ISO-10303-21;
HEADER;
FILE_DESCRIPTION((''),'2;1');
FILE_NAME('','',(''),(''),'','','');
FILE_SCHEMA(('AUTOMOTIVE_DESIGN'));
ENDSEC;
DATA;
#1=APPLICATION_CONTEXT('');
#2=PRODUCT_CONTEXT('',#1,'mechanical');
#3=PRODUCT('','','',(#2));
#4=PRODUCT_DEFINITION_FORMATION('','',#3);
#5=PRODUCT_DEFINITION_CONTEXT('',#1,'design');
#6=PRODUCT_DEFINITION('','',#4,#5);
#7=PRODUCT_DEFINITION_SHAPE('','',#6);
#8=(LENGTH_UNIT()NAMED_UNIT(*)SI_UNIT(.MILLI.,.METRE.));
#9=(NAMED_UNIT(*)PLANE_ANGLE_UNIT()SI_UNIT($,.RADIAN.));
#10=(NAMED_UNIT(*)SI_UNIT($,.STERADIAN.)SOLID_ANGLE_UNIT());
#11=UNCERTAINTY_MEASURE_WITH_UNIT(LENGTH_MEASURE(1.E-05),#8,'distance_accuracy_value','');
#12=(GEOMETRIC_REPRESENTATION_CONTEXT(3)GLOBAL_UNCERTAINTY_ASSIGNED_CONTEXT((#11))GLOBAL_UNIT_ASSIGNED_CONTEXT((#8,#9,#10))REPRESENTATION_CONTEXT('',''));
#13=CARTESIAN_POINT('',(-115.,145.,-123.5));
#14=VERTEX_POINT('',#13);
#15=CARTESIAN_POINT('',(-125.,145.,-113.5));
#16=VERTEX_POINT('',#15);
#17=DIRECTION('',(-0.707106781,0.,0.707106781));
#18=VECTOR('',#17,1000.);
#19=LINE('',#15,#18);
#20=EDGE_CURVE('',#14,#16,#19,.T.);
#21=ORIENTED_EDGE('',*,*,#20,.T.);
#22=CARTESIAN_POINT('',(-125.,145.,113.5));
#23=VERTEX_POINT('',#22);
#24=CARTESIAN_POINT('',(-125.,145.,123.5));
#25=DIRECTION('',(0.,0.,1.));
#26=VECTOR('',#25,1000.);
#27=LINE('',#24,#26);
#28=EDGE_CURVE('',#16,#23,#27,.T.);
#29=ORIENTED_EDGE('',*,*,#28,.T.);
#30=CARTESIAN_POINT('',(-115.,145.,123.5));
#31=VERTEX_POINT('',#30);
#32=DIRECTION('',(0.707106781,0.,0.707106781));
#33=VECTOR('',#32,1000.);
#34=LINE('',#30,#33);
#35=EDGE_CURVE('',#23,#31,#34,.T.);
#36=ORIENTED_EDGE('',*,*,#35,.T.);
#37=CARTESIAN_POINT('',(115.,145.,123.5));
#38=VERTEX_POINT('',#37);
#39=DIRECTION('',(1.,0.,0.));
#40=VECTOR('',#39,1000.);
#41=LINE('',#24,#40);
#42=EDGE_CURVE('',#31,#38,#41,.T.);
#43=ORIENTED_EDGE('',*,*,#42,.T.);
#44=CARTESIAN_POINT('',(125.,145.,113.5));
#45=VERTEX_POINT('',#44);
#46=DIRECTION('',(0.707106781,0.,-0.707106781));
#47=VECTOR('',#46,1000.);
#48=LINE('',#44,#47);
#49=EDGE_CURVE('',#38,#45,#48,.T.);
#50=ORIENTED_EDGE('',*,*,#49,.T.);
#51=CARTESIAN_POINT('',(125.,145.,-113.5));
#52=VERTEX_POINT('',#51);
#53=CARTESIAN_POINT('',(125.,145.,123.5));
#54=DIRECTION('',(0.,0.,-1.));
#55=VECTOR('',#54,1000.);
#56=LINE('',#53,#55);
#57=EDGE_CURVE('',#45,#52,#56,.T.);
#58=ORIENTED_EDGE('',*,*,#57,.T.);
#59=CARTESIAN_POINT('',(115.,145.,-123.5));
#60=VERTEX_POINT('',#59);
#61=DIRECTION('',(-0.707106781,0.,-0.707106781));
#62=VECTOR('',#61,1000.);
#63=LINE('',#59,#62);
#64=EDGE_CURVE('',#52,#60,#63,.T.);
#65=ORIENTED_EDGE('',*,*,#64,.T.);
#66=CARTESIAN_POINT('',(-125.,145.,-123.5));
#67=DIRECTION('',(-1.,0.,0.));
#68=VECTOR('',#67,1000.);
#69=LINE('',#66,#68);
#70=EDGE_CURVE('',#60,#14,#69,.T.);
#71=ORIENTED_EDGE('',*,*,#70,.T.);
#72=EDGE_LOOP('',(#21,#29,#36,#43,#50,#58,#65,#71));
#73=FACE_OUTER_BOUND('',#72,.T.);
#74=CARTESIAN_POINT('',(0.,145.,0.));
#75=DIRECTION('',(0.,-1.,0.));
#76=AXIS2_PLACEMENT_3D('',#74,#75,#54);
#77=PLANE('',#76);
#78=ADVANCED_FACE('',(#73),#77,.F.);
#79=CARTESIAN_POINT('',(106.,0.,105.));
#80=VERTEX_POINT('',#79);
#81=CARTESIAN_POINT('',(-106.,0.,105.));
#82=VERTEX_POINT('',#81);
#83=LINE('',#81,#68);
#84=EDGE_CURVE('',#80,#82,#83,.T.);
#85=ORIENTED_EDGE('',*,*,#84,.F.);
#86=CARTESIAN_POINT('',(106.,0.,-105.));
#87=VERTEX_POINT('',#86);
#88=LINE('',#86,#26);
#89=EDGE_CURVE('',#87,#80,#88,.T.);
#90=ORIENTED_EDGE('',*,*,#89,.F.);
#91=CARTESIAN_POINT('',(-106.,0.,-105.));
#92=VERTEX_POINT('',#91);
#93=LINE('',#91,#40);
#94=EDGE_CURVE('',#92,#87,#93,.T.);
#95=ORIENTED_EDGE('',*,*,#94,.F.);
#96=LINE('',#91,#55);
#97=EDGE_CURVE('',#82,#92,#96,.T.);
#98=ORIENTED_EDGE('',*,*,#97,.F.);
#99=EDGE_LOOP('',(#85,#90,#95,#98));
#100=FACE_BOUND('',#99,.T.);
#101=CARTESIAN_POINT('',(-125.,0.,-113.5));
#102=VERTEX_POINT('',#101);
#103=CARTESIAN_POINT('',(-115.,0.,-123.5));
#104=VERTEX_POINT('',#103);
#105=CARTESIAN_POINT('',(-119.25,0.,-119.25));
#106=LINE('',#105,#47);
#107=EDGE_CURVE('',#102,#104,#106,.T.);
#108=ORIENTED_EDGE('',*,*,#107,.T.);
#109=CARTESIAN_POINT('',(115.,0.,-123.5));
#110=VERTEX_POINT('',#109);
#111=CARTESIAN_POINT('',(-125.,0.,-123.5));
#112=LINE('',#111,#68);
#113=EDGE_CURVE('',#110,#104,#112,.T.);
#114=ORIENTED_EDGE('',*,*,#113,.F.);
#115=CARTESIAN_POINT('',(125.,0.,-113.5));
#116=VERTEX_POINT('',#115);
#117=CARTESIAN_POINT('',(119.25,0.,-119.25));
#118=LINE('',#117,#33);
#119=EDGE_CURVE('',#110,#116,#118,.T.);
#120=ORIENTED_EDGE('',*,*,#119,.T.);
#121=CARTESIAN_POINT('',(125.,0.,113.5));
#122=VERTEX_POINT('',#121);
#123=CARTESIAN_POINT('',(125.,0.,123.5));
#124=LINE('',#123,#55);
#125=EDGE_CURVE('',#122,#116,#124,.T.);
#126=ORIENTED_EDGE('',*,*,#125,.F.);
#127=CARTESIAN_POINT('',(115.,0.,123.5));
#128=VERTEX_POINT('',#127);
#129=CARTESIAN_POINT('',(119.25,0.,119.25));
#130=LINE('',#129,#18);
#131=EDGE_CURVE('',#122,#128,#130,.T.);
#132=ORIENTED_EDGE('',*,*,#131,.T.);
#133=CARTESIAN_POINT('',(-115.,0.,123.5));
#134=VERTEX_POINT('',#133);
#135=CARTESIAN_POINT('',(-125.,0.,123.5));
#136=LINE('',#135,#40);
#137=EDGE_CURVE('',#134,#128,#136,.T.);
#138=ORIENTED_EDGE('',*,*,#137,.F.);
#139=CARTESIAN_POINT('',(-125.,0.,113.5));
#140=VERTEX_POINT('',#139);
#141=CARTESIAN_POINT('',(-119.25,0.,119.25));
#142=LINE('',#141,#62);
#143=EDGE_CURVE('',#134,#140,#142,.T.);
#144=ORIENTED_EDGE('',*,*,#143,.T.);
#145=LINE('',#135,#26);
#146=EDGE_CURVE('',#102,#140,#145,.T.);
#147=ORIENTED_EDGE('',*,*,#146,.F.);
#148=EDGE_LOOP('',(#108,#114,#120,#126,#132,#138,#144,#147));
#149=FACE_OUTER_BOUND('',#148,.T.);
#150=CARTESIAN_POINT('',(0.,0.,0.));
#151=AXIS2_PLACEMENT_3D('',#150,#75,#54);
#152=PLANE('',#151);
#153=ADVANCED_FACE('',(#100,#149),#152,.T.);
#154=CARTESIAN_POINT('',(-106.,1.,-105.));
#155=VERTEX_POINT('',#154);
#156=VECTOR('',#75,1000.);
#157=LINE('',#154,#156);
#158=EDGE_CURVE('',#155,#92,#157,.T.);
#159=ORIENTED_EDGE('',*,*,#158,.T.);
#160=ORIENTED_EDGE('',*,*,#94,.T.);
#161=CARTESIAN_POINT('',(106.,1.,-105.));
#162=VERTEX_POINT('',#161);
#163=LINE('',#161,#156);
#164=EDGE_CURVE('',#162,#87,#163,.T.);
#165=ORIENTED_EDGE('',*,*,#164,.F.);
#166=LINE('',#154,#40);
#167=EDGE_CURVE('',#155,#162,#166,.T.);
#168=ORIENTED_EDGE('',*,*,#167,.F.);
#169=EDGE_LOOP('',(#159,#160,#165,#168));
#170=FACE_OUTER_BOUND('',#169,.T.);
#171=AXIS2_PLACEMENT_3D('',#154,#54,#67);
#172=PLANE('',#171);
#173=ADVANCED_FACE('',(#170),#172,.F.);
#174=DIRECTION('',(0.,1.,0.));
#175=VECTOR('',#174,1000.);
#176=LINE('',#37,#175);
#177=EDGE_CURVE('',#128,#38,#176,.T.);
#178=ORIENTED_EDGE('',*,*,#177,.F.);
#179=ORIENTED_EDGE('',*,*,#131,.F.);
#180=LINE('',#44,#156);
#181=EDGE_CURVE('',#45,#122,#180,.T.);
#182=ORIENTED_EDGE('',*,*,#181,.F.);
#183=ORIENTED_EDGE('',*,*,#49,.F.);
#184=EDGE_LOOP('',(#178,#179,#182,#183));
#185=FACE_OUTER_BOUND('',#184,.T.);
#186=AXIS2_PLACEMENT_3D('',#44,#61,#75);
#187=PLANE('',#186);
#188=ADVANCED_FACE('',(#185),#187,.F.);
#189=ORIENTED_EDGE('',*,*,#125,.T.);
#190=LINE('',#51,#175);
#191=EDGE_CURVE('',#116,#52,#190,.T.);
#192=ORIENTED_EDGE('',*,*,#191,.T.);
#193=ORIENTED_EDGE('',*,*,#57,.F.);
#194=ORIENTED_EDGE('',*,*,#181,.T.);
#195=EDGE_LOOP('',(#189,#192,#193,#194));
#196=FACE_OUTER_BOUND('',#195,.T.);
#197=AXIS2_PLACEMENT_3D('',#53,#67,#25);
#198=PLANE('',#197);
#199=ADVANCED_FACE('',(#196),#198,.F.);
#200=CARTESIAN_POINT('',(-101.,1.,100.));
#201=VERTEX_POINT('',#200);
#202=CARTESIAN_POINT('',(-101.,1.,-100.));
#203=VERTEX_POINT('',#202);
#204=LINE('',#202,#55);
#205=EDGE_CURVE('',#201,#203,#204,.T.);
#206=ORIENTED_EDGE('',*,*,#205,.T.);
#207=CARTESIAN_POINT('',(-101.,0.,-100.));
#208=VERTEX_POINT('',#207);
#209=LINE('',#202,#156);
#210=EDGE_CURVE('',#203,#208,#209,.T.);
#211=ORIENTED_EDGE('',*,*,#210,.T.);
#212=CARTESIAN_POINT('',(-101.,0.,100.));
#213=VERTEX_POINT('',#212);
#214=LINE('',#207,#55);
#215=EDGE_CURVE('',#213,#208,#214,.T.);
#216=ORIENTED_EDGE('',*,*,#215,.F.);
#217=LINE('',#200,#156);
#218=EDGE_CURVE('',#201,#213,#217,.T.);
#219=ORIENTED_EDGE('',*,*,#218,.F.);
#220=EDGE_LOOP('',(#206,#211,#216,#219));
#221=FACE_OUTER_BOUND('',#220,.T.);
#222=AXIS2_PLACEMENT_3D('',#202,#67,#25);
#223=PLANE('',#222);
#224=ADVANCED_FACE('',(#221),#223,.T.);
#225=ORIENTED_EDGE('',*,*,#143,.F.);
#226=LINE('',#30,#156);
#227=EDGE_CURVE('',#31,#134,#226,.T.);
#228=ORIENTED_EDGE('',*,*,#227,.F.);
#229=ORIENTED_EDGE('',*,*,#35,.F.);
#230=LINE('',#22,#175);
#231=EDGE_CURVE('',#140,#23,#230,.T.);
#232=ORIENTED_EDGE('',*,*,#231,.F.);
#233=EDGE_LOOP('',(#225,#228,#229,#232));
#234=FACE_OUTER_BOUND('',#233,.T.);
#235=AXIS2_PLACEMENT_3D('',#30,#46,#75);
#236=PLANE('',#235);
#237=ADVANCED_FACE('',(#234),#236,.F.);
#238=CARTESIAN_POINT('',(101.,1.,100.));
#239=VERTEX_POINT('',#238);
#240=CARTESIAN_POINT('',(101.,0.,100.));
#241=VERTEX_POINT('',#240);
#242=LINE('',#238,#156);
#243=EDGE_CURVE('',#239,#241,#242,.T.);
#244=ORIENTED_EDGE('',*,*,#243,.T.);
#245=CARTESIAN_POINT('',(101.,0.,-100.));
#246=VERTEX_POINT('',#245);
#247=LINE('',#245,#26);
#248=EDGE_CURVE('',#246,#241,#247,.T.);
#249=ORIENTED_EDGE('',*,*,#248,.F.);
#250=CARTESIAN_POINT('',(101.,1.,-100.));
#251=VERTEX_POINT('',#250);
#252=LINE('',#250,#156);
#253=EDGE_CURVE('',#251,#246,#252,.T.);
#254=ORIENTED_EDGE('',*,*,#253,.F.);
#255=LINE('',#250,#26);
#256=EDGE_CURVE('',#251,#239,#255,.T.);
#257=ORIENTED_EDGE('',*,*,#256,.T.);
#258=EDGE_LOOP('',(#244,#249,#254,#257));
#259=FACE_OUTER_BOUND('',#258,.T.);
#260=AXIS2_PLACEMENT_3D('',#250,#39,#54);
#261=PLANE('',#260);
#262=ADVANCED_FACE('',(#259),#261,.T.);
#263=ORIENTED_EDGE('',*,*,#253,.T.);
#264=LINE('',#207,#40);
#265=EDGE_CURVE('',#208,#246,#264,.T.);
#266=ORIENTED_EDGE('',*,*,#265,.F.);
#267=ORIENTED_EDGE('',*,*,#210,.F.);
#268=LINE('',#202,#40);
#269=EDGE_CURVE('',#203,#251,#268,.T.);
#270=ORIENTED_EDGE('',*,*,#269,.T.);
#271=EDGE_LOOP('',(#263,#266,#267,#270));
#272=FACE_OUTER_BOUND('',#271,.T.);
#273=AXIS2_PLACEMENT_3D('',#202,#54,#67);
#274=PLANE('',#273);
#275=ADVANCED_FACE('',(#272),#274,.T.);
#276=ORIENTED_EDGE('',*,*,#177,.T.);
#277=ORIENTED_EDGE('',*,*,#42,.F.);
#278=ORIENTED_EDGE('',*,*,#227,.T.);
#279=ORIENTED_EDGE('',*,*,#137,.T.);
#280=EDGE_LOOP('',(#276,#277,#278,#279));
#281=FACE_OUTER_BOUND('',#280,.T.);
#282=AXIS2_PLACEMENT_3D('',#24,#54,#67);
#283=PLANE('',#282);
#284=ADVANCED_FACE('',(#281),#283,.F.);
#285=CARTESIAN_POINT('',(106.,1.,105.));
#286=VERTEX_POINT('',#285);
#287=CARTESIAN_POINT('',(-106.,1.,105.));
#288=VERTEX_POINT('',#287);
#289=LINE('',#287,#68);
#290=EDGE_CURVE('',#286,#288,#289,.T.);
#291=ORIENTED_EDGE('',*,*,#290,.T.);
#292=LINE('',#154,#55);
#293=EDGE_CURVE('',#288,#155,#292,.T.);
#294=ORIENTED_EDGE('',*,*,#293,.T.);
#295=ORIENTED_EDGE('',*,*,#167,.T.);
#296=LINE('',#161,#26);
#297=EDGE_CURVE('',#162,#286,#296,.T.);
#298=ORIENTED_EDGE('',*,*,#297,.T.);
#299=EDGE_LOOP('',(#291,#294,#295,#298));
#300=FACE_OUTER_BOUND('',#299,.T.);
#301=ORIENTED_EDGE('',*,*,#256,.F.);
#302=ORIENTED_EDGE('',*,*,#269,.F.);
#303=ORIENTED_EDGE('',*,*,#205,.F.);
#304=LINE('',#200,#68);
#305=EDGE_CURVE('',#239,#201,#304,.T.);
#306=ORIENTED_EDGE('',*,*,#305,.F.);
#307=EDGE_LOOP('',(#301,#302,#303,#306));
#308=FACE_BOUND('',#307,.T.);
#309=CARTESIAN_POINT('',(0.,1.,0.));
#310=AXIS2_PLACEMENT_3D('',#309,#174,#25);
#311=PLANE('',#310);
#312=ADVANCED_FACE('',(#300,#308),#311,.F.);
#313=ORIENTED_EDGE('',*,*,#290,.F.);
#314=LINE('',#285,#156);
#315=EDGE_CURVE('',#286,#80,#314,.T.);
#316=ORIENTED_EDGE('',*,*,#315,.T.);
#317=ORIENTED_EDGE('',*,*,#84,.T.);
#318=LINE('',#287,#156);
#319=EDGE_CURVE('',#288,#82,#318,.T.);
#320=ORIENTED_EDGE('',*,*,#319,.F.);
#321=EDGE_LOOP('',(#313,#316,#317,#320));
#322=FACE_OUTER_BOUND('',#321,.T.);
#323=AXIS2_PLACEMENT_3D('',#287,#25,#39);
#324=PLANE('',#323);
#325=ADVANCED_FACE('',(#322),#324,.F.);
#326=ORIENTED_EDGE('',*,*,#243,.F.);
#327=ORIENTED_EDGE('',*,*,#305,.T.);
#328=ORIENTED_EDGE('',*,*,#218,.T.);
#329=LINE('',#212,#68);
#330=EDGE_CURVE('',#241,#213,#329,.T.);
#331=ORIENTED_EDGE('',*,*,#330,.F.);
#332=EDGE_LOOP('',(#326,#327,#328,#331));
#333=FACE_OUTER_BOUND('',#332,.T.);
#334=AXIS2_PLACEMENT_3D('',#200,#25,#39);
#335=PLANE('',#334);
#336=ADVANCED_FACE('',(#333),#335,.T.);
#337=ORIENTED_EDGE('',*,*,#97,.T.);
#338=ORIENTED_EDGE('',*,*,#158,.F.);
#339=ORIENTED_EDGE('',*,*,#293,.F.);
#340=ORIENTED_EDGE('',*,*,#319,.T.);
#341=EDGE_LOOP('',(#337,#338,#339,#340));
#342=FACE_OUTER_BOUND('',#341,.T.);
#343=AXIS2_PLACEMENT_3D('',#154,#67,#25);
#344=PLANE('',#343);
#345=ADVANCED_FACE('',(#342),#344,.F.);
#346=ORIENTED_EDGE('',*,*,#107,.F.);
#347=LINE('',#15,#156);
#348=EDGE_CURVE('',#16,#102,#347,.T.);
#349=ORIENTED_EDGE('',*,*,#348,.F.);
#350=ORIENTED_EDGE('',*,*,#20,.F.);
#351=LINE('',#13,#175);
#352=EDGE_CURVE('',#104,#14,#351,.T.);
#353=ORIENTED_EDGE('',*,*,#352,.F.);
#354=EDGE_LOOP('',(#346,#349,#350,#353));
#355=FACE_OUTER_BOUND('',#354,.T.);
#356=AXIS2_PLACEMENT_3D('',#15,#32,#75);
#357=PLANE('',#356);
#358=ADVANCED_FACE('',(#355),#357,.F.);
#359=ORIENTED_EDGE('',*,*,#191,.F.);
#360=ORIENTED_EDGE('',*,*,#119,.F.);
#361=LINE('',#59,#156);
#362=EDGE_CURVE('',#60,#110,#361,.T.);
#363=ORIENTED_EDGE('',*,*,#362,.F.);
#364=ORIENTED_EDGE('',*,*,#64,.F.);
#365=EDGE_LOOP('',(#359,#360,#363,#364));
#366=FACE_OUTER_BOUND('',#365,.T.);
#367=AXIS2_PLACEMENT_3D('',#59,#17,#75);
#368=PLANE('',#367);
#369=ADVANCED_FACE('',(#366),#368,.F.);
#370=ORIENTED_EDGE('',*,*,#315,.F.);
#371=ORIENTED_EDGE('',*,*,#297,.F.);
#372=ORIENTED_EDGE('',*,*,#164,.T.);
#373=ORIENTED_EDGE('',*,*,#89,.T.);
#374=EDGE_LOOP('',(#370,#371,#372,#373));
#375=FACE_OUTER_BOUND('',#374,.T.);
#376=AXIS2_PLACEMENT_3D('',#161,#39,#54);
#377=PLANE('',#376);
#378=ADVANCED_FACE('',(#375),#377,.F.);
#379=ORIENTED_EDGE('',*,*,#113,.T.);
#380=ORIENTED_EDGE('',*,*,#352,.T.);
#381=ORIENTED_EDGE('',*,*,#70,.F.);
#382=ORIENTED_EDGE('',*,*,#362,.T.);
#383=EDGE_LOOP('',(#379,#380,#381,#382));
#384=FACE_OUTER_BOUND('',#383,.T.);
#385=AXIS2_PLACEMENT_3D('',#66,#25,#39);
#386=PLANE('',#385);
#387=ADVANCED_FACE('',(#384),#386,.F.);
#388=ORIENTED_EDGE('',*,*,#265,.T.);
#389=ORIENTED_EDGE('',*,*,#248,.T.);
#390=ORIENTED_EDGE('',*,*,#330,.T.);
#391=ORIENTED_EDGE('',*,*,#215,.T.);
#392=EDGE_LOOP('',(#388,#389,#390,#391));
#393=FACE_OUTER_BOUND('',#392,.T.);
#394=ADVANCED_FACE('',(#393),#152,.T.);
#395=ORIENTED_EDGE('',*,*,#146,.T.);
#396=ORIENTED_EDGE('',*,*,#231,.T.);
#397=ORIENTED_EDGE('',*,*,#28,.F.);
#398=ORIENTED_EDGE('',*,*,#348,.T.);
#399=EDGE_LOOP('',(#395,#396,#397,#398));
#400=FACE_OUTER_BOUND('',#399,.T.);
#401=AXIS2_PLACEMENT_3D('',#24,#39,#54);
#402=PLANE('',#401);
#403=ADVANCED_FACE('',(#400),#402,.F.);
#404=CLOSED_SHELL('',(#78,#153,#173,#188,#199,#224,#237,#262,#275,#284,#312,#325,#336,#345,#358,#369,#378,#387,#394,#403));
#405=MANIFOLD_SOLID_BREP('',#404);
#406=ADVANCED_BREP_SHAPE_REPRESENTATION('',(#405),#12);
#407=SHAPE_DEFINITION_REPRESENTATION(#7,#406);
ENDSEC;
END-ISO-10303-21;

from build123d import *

# Parameters (mm, degrees)
SKETCH1_W           = 250
SKETCH1_H           = 247
BOSS_EXTRUDE1_DEPTH = 145
CHAMFER1_SIZE       = 10
SKETCH3_W           = 212
SKETCH3_H           = 210
SKETCH3_W_2         = 202
SKETCH3_H_2         = 200
CUT_EXTRUDE2_DEPTH  = 1


with BuildPart() as part:
    # Sketch1 → Boss-Extrude1 (new body)
    with BuildSketch(Plane(origin=(0, 0, 0), x_dir=(1, 0, 0), z_dir=(0, 1, 0))):
        Rectangle(SKETCH1_W, SKETCH1_H)
    extrude(amount=BOSS_EXTRUDE1_DEPTH)

    # Chamfer1
    chamfer1_edges = [part.edges().sort_by_distance(p)[0] for p in [
        (125, 72.5, 123.5),
        (-125, 72.5, 123.5),
        (-125, 72.5, -123.5),
        (125, 72.5, -123.5),
    ]]
    chamfer(chamfer1_edges, length=CHAMFER1_SIZE)

    # Sketch3 → Cut-Extrude2 (cut)
    with BuildSketch(Plane.XZ):
        Rectangle(SKETCH3_W, SKETCH3_H)
        Rectangle(SKETCH3_W_2, SKETCH3_H_2, mode=Mode.SUBTRACT)
    extrude(amount=-CUT_EXTRUDE2_DEPTH, mode=Mode.SUBTRACT)


solid = part.part
